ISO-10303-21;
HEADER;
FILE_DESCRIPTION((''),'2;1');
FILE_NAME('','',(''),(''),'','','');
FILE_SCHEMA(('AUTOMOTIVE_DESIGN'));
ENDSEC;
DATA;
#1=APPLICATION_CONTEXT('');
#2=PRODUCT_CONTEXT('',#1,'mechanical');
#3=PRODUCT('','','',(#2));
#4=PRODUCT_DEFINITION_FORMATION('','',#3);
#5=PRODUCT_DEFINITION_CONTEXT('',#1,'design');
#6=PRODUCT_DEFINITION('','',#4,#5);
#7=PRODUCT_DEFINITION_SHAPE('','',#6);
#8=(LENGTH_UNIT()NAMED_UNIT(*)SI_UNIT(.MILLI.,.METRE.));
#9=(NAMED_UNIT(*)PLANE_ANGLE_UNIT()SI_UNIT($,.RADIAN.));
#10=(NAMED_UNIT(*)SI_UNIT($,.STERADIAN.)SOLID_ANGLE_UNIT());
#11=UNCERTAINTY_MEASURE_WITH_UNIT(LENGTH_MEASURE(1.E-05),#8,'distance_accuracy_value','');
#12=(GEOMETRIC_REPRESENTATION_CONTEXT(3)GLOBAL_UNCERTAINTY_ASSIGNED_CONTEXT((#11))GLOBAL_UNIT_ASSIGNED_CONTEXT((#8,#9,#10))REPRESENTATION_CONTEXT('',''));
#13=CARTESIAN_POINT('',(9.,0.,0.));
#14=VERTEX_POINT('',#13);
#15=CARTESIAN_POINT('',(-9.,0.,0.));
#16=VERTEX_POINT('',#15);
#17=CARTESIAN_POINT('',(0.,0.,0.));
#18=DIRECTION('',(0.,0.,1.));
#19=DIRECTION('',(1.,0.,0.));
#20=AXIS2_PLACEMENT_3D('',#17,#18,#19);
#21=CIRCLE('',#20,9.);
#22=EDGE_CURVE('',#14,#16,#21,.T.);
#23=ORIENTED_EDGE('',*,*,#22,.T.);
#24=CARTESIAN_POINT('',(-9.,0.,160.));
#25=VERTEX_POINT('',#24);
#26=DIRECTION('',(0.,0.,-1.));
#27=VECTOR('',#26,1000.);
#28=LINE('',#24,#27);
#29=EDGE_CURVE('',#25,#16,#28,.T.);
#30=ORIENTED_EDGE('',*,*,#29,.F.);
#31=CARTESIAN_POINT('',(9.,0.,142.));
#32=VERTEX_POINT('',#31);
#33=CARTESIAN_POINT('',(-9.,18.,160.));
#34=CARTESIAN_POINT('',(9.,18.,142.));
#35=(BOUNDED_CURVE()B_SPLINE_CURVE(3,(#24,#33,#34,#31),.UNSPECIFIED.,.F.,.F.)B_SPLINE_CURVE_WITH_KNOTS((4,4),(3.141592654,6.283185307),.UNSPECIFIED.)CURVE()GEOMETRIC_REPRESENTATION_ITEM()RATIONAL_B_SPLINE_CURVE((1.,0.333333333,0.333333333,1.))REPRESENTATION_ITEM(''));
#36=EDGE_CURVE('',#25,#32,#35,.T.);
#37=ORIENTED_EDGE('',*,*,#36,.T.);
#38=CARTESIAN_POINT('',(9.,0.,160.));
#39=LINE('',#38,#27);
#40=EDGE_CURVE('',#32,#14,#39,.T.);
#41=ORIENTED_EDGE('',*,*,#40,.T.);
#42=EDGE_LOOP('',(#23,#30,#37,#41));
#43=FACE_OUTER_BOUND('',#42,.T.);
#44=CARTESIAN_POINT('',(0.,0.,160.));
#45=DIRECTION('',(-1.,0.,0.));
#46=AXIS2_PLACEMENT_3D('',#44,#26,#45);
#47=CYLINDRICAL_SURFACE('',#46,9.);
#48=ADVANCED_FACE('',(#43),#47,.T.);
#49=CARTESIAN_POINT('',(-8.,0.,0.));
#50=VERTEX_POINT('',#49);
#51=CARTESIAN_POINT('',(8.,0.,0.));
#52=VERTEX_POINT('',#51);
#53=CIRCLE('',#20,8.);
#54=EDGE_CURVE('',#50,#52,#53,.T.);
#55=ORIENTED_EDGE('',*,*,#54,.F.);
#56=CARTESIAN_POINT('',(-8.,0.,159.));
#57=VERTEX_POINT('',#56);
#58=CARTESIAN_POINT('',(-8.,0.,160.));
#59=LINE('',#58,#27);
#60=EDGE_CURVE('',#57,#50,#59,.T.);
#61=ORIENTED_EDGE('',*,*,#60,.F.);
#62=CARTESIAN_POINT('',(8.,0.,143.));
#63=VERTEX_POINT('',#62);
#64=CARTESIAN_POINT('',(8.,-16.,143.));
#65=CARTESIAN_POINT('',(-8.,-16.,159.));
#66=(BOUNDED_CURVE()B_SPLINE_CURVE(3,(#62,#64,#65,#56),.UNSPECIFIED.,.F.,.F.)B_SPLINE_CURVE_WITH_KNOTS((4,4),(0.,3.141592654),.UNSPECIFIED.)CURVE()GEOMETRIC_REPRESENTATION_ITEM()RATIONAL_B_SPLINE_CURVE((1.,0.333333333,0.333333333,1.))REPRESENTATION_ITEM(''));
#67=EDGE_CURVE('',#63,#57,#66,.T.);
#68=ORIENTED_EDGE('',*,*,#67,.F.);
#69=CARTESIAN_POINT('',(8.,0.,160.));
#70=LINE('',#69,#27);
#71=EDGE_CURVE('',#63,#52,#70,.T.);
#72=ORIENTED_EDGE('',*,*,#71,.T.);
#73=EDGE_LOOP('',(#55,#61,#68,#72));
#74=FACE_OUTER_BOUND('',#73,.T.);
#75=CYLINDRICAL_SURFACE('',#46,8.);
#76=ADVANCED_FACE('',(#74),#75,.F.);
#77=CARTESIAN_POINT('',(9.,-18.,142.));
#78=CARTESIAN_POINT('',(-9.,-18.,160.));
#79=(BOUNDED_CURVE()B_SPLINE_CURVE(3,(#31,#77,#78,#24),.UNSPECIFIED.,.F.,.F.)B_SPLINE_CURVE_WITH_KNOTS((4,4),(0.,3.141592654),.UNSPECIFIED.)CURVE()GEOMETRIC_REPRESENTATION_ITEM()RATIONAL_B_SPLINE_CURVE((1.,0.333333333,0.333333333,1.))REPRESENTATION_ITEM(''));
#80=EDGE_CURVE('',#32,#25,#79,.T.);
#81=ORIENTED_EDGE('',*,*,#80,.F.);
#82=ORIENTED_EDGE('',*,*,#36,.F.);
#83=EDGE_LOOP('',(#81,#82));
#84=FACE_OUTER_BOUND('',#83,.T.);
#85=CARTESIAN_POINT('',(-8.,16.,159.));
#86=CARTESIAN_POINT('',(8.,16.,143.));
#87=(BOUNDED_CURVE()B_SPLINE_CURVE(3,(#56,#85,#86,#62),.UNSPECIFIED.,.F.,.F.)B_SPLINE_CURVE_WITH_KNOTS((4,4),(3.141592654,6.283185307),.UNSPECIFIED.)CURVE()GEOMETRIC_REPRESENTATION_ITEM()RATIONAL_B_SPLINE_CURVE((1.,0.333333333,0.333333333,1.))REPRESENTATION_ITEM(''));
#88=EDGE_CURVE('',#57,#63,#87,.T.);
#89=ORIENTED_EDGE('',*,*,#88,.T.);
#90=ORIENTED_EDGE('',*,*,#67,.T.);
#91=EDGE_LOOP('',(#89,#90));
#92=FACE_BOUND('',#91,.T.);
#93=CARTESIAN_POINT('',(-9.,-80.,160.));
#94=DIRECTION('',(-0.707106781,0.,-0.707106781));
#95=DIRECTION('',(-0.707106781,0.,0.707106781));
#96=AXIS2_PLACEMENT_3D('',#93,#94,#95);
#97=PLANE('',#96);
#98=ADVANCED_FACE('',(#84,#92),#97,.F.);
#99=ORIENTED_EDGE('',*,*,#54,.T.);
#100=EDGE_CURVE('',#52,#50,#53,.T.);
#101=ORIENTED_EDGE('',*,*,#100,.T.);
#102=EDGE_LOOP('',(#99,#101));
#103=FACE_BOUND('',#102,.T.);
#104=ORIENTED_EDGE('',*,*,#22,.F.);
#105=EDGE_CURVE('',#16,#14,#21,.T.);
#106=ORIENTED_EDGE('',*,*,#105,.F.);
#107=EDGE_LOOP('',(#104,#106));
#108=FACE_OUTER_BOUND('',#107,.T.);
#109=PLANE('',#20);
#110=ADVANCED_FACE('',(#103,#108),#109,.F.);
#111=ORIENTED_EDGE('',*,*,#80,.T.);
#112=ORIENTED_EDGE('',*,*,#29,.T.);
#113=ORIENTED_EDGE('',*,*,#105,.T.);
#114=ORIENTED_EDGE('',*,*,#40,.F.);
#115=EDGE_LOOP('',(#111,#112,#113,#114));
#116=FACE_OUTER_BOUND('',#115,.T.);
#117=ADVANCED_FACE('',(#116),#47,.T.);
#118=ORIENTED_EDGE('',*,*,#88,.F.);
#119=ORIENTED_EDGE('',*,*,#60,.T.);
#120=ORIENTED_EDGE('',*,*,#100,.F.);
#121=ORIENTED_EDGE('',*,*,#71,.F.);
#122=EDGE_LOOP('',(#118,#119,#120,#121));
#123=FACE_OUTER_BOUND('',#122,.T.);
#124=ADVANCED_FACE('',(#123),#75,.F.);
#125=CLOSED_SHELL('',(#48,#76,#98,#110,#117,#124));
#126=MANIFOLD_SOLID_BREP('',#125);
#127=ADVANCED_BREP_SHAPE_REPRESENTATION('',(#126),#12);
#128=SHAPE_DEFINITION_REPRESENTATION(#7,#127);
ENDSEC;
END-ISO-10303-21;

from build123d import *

# Parameters (mm, degrees)
SKETCH1_R           = 9
SKETCH1_R_2         = 8
BOSS_EXTRUDE1_DEPTH = 160
CUT_EXTRUDE1_DEPTH  = 80


with BuildPart() as part:
    # Sketch1 → Boss-Extrude1 (new body)
    with BuildSketch(Plane.XY):
        Circle(SKETCH1_R)
        Circle(SKETCH1_R_2, mode=Mode.SUBTRACT)
    extrude(amount=BOSS_EXTRUDE1_DEPTH)

    # Sketch2 → Cut-Extrude1 (cut, symmetric)
    with BuildSketch(Plane(origin=(0, 0, 0), x_dir=(1, 0, 0), z_dir=(0, 1, 0))):
        Polygon((-9, -160), (9, -142), (9, -160), align=None)
    extrude(amount=CUT_EXTRUDE1_DEPTH, both=True, mode=Mode.SUBTRACT)


solid = part.part
